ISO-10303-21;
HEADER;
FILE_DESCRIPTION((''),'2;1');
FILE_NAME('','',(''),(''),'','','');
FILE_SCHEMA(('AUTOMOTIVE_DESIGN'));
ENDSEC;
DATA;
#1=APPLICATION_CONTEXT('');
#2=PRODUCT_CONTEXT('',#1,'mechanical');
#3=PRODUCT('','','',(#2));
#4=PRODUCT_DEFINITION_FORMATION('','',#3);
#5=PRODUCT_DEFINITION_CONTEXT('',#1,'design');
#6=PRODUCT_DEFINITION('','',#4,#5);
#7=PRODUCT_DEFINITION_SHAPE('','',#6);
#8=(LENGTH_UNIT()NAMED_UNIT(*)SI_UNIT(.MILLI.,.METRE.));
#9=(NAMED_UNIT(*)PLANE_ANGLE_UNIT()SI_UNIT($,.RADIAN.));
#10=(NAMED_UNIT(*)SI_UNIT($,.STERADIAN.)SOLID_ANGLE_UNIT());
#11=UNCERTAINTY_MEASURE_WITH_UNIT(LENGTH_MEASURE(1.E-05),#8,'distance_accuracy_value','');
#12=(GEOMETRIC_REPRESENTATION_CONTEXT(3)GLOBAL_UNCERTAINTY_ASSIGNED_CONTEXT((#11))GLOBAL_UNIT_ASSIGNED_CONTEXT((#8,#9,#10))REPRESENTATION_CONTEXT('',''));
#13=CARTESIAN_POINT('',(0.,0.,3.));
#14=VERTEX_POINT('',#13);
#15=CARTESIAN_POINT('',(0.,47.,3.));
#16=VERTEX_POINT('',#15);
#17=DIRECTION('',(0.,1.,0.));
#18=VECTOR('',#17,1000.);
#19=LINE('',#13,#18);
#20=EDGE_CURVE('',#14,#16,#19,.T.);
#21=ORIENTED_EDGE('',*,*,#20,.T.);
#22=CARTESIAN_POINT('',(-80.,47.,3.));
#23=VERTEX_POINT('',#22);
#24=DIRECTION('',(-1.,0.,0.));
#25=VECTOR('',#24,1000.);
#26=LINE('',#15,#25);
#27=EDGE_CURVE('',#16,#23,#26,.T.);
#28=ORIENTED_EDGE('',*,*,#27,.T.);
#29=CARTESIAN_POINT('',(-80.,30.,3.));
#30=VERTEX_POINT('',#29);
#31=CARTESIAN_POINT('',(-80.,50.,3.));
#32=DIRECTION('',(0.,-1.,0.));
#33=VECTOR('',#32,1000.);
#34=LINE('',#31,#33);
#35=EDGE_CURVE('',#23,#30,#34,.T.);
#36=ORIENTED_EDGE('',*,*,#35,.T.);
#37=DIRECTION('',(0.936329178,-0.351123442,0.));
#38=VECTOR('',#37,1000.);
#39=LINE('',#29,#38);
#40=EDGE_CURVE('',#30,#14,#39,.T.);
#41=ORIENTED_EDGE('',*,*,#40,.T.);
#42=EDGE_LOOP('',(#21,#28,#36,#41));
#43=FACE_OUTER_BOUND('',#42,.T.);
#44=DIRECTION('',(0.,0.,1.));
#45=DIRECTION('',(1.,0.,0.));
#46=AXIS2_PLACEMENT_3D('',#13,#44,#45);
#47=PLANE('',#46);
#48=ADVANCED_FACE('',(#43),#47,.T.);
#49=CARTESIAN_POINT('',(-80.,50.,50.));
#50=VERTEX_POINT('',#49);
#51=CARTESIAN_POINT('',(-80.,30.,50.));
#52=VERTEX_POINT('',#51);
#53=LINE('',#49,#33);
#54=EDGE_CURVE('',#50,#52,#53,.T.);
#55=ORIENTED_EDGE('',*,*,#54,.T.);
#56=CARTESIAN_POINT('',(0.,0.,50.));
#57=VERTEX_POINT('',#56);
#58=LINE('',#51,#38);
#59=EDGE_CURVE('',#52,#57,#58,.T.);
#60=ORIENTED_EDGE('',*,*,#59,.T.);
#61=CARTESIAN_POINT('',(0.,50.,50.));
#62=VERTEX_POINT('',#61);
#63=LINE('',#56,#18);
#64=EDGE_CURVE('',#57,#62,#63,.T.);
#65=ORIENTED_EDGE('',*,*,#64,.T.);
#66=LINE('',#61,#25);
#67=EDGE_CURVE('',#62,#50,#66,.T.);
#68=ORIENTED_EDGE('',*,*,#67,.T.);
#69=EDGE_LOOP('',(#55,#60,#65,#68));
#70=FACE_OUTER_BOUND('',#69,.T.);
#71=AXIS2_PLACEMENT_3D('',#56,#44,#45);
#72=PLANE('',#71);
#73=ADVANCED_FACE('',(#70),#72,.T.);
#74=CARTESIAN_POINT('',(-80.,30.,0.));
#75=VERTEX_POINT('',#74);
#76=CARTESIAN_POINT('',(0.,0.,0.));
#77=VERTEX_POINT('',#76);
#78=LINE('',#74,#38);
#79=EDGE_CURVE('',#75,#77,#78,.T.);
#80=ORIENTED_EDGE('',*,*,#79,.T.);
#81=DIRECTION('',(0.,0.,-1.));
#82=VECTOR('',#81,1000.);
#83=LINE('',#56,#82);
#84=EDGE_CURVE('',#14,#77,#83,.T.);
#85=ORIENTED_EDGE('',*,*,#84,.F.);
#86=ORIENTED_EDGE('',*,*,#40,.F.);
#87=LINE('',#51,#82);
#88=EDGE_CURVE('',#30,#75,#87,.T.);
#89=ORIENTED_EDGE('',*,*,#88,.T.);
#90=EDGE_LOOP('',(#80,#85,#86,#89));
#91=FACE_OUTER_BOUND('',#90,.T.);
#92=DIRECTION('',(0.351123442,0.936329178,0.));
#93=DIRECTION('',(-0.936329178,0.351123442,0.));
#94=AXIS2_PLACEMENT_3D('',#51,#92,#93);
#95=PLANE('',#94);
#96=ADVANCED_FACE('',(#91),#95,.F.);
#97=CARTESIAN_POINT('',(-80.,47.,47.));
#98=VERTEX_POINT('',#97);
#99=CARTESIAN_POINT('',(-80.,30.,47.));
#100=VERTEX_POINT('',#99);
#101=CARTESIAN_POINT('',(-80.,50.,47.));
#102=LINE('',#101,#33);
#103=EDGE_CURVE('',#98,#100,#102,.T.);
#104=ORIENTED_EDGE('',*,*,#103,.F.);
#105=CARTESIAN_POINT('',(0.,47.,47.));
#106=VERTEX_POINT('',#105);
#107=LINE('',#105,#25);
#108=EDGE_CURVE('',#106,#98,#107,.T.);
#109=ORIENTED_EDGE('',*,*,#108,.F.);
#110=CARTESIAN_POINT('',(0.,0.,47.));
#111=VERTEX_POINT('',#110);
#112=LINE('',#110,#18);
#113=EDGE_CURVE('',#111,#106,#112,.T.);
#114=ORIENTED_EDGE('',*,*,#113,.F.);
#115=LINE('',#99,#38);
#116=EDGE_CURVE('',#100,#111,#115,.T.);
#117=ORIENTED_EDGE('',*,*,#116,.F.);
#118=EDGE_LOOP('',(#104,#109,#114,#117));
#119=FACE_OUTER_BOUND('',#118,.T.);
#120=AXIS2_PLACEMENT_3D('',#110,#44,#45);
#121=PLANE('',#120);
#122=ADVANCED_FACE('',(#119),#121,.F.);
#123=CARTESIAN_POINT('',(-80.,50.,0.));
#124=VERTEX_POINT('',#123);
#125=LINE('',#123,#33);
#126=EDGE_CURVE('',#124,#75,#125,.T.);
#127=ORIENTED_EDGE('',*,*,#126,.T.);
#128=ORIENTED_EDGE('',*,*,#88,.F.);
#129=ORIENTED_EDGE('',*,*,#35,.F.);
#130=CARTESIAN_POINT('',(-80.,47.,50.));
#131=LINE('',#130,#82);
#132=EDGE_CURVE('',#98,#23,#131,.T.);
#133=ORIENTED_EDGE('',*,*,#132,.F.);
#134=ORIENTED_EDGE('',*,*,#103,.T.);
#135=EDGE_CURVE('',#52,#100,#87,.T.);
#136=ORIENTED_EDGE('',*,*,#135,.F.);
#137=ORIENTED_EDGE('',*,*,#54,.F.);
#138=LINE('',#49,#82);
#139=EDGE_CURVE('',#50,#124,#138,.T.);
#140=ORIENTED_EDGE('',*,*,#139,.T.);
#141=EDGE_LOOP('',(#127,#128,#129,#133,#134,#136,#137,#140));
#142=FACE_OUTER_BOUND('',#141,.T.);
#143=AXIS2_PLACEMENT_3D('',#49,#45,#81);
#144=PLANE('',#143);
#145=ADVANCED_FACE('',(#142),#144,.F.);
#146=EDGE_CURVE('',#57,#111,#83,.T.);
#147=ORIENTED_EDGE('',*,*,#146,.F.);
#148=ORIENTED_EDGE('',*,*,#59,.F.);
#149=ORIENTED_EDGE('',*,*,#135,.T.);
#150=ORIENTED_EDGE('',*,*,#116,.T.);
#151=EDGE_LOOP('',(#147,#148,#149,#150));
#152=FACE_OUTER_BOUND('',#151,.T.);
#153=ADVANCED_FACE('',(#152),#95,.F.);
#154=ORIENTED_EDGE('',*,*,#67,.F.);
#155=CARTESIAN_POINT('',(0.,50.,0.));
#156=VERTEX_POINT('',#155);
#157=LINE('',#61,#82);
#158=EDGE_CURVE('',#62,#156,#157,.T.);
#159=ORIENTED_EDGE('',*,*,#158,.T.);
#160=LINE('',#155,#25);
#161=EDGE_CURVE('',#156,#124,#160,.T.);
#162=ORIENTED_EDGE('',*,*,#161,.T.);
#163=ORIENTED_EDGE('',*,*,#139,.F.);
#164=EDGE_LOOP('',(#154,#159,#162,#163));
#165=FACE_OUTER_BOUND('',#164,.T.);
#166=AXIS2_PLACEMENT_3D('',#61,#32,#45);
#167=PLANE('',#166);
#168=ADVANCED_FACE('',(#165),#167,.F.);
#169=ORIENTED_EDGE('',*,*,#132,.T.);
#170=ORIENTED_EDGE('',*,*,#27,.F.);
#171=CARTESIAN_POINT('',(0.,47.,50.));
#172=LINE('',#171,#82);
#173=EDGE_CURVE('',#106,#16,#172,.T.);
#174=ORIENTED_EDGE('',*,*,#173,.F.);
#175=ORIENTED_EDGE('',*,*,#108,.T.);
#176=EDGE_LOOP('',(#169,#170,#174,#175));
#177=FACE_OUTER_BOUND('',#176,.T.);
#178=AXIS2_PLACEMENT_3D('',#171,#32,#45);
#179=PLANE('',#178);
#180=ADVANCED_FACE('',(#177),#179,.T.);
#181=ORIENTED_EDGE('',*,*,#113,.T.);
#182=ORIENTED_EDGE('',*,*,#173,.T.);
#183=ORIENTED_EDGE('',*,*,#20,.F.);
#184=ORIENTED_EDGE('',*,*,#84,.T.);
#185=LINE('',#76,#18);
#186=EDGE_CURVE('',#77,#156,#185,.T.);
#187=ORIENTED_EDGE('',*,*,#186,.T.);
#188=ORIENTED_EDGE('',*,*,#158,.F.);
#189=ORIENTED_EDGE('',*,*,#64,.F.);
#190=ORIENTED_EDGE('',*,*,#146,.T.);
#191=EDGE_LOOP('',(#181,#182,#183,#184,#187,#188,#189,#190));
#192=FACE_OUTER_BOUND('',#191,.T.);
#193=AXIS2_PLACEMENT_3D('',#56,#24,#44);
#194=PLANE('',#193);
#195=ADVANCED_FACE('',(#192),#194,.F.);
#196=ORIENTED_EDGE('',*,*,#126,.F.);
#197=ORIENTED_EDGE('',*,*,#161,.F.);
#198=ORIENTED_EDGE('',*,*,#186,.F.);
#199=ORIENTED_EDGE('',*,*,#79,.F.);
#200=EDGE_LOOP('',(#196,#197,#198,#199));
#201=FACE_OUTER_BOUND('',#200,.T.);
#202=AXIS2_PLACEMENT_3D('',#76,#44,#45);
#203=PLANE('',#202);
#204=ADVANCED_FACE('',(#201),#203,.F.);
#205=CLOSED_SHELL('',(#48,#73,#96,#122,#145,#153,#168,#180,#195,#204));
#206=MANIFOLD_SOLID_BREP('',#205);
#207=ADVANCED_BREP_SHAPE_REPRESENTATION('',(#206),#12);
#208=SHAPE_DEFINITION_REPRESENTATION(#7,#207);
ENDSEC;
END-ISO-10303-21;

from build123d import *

# Parameters (mm, degrees)
EXTRUDE_1_DEPTH = 50
SHELL_1_T       = -3


with BuildPart() as part:
    # 草图1 → 凸台-拉伸1 (new body)
    with BuildSketch(Plane.XY):
        Polygon((0, 0), (0, 50), (-80, 50), (-80, 30), align=None)
    extrude(amount=EXTRUDE_1_DEPTH)

    # 抽壳1
    shell_1_openings = [part.faces().sort_by_distance(p)[0] for p in [
        (-80, 40, 25),
        (0, 25, 25),
        (-40, 15, 25),
    ]]
    offset(amount=SHELL_1_T, openings=shell_1_openings, kind=Kind.INTERSECTION)


solid = part.part
